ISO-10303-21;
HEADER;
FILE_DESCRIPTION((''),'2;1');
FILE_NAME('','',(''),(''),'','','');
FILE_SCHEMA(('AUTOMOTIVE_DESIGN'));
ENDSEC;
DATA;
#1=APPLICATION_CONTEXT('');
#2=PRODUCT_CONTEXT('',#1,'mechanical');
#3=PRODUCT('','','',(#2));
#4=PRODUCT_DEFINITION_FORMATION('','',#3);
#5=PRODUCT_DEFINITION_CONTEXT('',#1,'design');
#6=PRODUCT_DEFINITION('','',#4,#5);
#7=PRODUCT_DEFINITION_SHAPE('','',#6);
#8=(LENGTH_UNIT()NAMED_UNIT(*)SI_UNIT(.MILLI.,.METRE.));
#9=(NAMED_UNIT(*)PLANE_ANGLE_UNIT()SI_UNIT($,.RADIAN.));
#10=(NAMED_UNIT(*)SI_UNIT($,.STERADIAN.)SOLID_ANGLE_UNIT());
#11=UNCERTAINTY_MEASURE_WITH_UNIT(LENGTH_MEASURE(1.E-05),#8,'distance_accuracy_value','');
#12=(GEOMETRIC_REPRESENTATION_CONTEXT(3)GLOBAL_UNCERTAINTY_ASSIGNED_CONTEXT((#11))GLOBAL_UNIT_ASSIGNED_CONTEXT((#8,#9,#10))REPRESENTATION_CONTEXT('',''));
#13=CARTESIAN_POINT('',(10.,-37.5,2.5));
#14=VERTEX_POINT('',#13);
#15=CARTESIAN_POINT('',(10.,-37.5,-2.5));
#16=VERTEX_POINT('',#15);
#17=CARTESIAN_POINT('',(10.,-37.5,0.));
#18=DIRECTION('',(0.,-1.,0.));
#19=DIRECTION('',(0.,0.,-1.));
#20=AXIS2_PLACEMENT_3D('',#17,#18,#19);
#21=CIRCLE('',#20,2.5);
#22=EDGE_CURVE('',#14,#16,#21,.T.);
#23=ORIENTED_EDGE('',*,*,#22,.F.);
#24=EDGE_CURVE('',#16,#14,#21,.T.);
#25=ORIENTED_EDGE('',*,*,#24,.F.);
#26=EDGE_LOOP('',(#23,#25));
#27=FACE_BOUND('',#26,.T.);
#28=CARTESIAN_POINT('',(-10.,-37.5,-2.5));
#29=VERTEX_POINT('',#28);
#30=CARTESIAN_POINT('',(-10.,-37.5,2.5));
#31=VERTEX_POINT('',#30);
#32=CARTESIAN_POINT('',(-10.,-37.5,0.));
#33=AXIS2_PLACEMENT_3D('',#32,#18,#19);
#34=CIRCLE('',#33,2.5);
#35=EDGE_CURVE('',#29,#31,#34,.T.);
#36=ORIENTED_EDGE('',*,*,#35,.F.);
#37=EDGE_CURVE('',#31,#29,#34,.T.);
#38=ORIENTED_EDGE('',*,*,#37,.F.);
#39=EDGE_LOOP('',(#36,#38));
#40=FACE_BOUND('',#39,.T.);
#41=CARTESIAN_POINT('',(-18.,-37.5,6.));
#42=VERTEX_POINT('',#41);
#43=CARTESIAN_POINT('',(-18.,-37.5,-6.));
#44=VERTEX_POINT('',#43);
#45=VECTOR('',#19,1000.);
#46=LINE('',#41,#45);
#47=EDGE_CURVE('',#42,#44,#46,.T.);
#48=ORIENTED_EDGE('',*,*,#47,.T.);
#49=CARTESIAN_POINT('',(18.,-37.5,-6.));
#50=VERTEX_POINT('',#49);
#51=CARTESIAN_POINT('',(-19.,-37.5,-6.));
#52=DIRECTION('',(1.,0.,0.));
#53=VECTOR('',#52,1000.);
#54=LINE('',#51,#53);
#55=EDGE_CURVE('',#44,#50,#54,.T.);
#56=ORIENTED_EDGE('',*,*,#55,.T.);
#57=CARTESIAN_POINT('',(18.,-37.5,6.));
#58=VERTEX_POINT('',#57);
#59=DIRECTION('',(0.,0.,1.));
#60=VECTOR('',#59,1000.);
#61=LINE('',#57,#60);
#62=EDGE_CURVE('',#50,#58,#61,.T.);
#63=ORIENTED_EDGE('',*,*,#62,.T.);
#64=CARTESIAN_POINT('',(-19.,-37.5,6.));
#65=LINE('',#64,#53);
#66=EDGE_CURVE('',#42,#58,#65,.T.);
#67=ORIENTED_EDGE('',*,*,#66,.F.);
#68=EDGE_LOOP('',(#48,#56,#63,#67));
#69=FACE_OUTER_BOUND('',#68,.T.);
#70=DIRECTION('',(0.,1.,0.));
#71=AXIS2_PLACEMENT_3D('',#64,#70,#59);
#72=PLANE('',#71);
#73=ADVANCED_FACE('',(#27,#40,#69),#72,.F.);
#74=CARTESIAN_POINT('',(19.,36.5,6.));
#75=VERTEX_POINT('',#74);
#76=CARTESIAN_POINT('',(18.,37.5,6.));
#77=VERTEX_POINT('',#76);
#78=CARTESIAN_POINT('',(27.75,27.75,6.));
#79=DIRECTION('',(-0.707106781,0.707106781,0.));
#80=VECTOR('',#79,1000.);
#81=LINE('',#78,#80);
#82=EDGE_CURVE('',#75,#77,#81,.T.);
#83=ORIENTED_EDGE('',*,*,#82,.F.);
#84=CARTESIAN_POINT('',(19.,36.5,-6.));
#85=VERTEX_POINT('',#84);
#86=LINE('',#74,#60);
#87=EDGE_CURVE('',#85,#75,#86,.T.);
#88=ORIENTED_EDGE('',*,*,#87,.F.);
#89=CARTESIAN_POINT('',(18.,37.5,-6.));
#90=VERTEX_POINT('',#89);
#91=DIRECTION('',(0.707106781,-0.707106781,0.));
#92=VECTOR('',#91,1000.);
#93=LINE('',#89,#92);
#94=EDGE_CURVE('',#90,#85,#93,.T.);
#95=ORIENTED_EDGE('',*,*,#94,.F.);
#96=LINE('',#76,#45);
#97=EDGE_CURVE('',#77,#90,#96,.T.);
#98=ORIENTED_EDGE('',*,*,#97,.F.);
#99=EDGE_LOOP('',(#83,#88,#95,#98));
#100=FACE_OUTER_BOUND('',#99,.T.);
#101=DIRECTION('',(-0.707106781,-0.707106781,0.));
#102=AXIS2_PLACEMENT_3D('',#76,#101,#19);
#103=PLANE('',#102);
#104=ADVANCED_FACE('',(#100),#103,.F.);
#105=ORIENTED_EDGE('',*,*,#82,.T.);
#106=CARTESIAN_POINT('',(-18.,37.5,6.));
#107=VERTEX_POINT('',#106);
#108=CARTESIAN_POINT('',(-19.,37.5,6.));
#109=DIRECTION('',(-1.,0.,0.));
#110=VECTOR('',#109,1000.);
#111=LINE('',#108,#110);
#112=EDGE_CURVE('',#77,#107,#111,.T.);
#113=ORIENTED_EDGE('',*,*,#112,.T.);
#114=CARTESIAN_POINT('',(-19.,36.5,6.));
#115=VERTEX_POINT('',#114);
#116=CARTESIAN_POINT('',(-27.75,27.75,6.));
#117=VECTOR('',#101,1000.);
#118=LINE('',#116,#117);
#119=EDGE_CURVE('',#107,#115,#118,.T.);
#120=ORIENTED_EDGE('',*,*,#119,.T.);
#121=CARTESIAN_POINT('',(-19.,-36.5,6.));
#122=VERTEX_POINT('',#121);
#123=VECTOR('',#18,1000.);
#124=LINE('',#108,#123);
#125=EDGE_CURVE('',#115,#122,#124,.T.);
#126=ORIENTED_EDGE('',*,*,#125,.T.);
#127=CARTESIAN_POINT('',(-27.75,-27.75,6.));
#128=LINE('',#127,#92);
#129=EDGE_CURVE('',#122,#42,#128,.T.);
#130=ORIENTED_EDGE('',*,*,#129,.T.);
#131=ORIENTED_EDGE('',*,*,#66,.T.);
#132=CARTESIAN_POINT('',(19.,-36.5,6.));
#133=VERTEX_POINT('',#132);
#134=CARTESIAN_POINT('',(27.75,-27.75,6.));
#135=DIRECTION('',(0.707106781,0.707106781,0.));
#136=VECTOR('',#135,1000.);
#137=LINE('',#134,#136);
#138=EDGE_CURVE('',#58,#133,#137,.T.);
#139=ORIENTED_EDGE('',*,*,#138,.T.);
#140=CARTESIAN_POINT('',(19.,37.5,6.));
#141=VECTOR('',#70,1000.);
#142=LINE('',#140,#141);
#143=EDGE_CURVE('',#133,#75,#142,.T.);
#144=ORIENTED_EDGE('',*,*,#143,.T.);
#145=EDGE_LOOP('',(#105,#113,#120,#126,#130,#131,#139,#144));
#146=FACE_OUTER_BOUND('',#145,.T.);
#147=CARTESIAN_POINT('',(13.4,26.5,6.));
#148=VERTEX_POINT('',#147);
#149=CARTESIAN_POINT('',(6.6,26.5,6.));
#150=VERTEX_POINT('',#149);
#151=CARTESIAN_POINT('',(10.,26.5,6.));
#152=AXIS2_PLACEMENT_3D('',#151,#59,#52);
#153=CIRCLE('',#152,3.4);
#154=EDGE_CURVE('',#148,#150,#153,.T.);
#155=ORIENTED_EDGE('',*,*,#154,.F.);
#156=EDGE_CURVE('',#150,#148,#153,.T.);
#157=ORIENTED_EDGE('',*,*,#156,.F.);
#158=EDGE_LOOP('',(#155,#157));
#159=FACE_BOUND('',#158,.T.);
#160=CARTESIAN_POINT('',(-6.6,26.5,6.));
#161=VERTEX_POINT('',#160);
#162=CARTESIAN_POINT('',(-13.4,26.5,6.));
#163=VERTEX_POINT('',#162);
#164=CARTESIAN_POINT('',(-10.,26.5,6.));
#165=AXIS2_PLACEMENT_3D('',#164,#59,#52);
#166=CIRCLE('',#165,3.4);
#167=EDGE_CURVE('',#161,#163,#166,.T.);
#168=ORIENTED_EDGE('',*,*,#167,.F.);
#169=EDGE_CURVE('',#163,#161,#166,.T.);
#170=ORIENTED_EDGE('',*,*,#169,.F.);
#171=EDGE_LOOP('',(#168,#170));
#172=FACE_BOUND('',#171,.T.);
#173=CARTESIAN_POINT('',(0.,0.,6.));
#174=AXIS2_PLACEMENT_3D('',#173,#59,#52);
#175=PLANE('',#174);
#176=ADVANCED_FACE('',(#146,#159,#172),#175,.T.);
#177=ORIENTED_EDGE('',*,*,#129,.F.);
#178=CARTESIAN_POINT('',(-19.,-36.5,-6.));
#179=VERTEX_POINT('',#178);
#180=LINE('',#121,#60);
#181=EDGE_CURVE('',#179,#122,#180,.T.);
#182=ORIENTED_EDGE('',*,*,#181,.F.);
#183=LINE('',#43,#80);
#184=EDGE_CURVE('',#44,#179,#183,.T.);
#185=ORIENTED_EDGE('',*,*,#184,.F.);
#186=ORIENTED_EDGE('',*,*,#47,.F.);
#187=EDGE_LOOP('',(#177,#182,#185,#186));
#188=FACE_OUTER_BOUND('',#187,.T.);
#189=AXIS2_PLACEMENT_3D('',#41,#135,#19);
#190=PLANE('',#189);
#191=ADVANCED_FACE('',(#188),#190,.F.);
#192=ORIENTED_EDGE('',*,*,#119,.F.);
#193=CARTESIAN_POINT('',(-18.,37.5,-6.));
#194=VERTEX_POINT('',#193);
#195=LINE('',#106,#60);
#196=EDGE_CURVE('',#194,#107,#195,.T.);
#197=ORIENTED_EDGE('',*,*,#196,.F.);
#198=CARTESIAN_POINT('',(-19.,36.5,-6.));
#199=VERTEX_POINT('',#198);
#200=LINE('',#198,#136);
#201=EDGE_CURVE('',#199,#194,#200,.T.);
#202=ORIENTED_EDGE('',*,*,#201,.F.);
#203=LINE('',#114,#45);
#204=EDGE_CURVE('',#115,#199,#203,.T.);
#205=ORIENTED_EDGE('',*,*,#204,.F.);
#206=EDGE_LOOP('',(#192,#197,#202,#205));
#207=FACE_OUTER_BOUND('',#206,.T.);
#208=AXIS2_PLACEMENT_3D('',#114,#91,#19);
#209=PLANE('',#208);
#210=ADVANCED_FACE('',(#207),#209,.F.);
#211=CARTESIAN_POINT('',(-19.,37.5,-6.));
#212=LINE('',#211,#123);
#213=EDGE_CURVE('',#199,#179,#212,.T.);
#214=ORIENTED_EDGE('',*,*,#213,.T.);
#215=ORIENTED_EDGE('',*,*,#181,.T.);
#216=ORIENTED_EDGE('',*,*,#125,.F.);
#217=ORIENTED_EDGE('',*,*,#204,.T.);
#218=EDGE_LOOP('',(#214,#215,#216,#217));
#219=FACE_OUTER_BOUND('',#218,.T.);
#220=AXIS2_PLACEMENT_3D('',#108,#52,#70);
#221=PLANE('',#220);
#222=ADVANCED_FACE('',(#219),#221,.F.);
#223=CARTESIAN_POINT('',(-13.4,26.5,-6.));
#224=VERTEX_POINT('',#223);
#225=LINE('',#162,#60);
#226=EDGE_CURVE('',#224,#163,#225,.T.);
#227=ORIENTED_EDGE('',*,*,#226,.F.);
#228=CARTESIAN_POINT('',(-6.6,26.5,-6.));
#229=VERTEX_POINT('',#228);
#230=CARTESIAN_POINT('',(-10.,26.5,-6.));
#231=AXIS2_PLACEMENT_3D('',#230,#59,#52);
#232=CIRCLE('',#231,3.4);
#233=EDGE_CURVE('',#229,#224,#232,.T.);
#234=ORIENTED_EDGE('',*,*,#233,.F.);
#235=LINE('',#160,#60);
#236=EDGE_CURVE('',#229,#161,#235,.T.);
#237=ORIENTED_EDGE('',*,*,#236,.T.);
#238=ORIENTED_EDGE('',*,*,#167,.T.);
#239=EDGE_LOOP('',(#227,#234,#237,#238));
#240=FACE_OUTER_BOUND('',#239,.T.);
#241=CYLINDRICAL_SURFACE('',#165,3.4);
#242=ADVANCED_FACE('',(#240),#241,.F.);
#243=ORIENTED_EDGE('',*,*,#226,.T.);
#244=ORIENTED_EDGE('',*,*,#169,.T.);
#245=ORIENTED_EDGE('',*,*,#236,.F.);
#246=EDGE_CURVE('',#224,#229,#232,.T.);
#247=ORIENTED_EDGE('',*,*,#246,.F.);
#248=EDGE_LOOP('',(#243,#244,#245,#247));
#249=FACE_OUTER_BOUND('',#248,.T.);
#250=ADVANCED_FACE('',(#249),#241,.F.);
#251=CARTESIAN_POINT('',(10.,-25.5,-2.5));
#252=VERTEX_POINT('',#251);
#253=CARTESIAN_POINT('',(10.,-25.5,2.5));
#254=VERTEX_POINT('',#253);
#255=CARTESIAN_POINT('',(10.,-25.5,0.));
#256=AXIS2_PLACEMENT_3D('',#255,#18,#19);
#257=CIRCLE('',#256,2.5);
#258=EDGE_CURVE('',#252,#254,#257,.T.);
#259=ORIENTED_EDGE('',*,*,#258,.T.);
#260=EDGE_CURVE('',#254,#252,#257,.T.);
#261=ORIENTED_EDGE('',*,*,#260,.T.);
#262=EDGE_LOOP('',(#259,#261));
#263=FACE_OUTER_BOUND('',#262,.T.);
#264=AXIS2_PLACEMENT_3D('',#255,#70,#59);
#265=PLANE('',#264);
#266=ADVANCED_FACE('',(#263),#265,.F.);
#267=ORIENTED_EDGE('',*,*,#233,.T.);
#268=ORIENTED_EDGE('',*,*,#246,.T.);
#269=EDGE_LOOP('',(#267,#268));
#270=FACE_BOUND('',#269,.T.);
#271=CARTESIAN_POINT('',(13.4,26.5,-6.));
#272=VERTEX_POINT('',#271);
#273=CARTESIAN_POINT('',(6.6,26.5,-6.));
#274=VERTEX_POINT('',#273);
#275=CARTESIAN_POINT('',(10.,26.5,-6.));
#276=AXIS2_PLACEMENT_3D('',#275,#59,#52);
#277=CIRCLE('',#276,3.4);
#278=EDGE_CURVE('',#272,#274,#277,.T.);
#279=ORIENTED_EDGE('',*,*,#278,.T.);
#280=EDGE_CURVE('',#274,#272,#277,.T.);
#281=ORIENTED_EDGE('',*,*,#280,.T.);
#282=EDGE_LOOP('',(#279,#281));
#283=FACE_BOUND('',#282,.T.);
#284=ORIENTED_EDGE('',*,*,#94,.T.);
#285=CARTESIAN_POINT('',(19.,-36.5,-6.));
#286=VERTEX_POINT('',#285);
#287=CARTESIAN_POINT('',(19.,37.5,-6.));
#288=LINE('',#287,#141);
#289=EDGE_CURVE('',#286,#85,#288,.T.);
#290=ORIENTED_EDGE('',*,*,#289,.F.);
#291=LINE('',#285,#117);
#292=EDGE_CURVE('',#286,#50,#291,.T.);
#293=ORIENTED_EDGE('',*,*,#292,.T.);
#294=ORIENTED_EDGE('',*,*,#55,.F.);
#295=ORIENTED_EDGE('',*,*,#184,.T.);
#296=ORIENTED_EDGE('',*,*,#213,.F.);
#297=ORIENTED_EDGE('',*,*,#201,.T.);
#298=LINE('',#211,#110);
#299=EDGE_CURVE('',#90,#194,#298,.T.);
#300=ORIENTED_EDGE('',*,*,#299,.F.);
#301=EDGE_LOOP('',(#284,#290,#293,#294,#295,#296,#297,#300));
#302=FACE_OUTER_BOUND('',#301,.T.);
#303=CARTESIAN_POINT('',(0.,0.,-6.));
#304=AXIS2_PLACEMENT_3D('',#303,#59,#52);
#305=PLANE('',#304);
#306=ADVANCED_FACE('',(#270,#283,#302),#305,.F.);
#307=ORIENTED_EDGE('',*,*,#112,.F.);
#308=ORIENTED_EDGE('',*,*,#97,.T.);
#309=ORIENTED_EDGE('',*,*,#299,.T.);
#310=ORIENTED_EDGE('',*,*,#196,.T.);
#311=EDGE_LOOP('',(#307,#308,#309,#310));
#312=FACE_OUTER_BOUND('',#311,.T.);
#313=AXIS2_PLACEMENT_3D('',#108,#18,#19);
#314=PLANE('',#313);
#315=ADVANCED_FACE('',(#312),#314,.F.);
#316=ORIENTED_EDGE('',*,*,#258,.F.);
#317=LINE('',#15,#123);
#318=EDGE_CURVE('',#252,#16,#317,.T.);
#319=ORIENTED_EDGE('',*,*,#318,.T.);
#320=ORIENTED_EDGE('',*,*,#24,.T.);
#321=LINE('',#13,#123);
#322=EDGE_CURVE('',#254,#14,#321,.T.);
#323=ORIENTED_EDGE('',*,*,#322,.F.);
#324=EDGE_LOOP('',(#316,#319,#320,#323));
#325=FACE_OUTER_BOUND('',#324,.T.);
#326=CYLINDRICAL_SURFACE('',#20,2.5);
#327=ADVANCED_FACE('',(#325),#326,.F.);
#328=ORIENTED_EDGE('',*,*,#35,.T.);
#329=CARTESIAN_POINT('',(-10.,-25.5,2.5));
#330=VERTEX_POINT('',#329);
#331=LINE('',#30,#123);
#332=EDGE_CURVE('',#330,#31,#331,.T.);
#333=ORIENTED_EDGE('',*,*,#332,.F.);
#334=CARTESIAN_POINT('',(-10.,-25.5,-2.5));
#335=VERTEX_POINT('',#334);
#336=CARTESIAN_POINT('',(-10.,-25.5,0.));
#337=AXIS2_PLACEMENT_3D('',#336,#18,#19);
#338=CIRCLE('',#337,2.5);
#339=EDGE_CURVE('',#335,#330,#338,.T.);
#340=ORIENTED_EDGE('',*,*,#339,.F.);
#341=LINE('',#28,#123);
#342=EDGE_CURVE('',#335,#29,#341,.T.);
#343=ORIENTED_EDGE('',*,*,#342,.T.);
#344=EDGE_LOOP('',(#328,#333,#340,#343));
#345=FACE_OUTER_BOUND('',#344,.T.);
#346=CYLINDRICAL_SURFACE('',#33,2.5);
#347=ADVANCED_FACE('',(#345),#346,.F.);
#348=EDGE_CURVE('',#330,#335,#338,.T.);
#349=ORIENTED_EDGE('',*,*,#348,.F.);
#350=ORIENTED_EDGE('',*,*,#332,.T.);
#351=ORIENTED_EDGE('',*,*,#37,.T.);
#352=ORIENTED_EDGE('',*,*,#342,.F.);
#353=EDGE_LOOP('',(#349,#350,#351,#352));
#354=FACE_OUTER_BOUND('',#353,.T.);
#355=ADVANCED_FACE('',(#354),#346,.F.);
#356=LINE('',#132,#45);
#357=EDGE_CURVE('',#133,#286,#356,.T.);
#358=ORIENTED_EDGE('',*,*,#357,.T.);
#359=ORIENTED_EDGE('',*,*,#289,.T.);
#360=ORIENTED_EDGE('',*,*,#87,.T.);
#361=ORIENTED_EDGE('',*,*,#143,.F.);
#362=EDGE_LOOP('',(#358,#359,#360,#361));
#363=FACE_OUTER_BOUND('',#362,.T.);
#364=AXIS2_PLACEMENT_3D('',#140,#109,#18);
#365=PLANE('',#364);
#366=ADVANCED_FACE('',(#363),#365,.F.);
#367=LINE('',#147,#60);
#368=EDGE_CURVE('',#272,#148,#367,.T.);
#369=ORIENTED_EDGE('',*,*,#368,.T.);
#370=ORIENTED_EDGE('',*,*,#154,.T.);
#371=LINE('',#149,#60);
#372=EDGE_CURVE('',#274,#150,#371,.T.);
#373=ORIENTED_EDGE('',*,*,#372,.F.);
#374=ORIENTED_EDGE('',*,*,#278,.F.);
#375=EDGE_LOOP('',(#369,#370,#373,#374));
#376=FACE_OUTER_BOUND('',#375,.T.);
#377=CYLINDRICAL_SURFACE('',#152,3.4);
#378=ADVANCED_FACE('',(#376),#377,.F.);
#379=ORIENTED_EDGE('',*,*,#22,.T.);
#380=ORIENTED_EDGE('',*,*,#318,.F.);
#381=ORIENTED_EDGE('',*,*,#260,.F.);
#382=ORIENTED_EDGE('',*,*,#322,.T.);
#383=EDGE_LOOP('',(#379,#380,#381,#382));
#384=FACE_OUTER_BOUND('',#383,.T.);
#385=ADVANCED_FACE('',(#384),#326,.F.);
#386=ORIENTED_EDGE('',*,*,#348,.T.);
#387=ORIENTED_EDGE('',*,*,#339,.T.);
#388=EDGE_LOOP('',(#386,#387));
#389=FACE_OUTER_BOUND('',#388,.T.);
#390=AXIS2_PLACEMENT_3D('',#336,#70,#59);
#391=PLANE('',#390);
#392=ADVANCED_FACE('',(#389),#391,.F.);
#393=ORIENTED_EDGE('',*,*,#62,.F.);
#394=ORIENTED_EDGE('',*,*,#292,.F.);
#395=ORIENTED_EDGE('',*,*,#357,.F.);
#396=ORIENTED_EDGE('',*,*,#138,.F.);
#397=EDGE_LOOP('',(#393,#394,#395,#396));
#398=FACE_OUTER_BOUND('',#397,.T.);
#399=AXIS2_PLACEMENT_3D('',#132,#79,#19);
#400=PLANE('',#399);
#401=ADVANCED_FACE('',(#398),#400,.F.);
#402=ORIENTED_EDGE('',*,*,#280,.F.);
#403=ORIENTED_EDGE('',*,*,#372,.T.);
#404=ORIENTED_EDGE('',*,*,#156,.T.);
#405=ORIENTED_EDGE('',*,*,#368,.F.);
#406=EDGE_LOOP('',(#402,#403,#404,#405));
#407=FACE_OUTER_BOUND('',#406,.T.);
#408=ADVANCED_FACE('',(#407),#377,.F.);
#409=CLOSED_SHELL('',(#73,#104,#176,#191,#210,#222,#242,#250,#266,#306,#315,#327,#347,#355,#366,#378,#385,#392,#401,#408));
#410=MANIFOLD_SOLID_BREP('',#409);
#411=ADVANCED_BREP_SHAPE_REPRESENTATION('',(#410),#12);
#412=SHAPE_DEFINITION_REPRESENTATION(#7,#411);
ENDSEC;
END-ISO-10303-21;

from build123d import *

# Parameters (mm, degrees)
SKETCH1_W             = 38
SKETCH1_H             = 75
BOSS_EXTRUDE1_DEPTH   = 6
M8_TAPPED_HOLE1_D     = 6.8
M8_TAPPED_HOLE2_D     = 6.8
M6_TAPPED_HOLE1_D     = 5
M6_TAPPED_HOLE1_DEPTH = 12
CHAMFER1_SIZE         = 1


with BuildPart() as part:
    # Sketch1 → Boss-Extrude1 (new, symmetric)
    with BuildSketch(Plane.XY):
        Rectangle(SKETCH1_W, SKETCH1_H)
    extrude(amount=BOSS_EXTRUDE1_DEPTH, both=True)

    # M8 Tapped Hole1 (through all)
    with Locations(Plane.XY.offset(6)):
        with Locations((-10, 26.5)):
            Hole(M8_TAPPED_HOLE1_D / 2)

    # M8 Tapped Hole2 (through all)
    with Locations(Plane.XY.offset(6)):
        with Locations((10, 26.5)):
            Hole(M8_TAPPED_HOLE2_D / 2)

    # M6 Tapped Hole1
    with Locations(Plane(origin=(0, -37.5, 0), x_dir=(-1, 0, 0), z_dir=(0, -1, 0))):
        with Locations((10, 0), (-10, 0)):
            Hole(M6_TAPPED_HOLE1_D / 2, depth=M6_TAPPED_HOLE1_DEPTH)

    # Chamfer1
    chamfer1_edges = [part.edges().sort_by_distance(p)[0] for p in [
        (19, -37.5, 0),
        (-19, -37.5, 0),
        (-19, 37.5, 0),
        (19, 37.5, 0),
    ]]
    chamfer(chamfer1_edges, length=CHAMFER1_SIZE)


solid = part.part
